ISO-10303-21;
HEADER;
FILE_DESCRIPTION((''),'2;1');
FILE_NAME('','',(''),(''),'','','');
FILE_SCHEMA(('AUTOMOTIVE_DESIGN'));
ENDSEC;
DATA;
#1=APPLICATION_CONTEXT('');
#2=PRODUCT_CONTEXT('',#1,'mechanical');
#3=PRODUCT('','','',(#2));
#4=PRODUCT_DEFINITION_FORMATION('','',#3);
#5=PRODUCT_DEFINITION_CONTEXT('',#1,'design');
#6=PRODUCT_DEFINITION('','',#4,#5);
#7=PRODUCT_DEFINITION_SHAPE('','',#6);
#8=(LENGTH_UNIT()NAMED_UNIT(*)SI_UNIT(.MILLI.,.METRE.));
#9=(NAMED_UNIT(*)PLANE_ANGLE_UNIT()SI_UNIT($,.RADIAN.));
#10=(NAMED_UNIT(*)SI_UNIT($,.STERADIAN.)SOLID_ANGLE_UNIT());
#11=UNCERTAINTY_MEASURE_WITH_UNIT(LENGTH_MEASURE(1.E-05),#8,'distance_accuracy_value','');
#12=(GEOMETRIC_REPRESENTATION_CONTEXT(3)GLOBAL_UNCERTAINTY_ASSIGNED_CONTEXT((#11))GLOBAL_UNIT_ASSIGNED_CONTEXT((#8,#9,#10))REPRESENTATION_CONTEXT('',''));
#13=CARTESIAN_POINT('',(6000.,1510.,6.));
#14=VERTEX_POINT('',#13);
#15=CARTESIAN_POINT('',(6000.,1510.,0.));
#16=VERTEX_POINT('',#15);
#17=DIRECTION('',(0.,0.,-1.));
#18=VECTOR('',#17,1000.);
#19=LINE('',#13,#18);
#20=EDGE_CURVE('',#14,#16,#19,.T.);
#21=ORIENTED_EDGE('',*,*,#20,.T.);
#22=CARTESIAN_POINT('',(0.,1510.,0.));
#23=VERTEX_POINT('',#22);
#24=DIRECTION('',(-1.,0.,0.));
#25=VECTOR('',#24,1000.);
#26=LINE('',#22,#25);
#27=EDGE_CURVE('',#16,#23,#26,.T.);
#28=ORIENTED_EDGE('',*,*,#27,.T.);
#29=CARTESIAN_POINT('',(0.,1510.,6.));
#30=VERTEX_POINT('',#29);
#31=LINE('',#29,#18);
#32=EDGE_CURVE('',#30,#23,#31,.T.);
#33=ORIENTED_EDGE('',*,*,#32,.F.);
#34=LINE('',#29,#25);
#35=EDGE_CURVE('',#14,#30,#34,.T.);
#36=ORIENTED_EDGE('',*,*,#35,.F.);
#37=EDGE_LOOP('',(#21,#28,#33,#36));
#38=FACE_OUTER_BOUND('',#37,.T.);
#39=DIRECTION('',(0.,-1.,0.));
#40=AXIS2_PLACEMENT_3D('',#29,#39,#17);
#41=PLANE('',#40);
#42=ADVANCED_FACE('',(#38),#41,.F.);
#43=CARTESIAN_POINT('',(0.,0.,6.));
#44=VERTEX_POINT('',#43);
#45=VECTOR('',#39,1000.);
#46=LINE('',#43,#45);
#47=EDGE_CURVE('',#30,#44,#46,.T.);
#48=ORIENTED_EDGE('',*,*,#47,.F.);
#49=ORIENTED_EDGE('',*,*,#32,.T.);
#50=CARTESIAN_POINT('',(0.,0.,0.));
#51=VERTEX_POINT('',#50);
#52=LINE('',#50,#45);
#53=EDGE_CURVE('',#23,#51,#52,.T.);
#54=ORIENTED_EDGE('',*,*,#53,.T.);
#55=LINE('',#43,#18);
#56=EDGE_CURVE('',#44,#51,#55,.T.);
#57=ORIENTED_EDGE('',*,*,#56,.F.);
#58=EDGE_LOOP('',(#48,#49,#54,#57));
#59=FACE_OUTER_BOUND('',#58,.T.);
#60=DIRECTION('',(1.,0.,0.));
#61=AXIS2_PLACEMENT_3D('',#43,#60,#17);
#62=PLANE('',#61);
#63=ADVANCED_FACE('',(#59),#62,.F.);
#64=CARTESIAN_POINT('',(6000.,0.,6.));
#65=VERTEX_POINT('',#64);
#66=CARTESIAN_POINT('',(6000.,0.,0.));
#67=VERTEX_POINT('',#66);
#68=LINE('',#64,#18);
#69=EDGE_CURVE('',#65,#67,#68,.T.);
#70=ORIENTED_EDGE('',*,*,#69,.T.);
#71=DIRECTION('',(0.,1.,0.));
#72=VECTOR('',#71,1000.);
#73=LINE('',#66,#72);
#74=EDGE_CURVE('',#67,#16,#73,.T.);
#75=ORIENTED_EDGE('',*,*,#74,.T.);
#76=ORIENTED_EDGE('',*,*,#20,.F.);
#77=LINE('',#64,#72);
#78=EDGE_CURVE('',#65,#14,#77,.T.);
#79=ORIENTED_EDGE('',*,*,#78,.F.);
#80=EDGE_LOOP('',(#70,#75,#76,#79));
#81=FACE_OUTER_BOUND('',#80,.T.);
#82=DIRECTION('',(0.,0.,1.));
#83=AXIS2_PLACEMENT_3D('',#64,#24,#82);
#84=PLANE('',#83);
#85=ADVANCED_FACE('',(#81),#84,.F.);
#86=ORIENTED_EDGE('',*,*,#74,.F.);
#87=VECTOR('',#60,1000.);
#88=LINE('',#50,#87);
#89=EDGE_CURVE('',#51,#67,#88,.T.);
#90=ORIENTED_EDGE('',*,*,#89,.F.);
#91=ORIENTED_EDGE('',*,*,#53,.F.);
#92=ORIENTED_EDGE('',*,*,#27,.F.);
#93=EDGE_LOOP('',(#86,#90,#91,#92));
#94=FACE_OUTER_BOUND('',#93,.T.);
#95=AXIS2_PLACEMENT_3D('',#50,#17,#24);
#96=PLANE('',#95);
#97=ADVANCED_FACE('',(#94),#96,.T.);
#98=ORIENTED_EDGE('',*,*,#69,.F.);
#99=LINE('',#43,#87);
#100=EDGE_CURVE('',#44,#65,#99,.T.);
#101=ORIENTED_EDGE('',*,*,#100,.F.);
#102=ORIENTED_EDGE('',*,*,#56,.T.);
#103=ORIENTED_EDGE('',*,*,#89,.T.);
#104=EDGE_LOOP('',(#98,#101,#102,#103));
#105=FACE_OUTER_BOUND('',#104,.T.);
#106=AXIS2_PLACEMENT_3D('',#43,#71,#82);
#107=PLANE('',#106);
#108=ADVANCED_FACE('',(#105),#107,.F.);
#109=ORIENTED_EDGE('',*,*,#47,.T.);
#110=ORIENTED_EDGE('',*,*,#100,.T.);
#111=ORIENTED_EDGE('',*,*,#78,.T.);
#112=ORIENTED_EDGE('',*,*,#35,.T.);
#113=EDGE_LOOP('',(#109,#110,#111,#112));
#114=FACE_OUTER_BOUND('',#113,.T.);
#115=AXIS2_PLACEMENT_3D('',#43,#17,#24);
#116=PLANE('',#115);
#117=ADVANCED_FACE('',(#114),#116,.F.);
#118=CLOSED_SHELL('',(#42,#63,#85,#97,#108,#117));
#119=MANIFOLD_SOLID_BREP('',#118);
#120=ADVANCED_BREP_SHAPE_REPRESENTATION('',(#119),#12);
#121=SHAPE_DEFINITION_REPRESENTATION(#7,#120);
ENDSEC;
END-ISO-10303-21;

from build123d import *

# Parameters (mm, degrees)
SKETCH1_W           = 6000
SKETCH1_H           = 1510
BOSS_EXTRUDE1_DEPTH = 6


with BuildPart() as part:
    # Sketch1 → Boss-Extrude1 (new body)
    with BuildSketch(Plane.XY):
        with Locations((3000, 755)):
            Rectangle(SKETCH1_W, SKETCH1_H)
    extrude(amount=BOSS_EXTRUDE1_DEPTH)


solid = part.part
